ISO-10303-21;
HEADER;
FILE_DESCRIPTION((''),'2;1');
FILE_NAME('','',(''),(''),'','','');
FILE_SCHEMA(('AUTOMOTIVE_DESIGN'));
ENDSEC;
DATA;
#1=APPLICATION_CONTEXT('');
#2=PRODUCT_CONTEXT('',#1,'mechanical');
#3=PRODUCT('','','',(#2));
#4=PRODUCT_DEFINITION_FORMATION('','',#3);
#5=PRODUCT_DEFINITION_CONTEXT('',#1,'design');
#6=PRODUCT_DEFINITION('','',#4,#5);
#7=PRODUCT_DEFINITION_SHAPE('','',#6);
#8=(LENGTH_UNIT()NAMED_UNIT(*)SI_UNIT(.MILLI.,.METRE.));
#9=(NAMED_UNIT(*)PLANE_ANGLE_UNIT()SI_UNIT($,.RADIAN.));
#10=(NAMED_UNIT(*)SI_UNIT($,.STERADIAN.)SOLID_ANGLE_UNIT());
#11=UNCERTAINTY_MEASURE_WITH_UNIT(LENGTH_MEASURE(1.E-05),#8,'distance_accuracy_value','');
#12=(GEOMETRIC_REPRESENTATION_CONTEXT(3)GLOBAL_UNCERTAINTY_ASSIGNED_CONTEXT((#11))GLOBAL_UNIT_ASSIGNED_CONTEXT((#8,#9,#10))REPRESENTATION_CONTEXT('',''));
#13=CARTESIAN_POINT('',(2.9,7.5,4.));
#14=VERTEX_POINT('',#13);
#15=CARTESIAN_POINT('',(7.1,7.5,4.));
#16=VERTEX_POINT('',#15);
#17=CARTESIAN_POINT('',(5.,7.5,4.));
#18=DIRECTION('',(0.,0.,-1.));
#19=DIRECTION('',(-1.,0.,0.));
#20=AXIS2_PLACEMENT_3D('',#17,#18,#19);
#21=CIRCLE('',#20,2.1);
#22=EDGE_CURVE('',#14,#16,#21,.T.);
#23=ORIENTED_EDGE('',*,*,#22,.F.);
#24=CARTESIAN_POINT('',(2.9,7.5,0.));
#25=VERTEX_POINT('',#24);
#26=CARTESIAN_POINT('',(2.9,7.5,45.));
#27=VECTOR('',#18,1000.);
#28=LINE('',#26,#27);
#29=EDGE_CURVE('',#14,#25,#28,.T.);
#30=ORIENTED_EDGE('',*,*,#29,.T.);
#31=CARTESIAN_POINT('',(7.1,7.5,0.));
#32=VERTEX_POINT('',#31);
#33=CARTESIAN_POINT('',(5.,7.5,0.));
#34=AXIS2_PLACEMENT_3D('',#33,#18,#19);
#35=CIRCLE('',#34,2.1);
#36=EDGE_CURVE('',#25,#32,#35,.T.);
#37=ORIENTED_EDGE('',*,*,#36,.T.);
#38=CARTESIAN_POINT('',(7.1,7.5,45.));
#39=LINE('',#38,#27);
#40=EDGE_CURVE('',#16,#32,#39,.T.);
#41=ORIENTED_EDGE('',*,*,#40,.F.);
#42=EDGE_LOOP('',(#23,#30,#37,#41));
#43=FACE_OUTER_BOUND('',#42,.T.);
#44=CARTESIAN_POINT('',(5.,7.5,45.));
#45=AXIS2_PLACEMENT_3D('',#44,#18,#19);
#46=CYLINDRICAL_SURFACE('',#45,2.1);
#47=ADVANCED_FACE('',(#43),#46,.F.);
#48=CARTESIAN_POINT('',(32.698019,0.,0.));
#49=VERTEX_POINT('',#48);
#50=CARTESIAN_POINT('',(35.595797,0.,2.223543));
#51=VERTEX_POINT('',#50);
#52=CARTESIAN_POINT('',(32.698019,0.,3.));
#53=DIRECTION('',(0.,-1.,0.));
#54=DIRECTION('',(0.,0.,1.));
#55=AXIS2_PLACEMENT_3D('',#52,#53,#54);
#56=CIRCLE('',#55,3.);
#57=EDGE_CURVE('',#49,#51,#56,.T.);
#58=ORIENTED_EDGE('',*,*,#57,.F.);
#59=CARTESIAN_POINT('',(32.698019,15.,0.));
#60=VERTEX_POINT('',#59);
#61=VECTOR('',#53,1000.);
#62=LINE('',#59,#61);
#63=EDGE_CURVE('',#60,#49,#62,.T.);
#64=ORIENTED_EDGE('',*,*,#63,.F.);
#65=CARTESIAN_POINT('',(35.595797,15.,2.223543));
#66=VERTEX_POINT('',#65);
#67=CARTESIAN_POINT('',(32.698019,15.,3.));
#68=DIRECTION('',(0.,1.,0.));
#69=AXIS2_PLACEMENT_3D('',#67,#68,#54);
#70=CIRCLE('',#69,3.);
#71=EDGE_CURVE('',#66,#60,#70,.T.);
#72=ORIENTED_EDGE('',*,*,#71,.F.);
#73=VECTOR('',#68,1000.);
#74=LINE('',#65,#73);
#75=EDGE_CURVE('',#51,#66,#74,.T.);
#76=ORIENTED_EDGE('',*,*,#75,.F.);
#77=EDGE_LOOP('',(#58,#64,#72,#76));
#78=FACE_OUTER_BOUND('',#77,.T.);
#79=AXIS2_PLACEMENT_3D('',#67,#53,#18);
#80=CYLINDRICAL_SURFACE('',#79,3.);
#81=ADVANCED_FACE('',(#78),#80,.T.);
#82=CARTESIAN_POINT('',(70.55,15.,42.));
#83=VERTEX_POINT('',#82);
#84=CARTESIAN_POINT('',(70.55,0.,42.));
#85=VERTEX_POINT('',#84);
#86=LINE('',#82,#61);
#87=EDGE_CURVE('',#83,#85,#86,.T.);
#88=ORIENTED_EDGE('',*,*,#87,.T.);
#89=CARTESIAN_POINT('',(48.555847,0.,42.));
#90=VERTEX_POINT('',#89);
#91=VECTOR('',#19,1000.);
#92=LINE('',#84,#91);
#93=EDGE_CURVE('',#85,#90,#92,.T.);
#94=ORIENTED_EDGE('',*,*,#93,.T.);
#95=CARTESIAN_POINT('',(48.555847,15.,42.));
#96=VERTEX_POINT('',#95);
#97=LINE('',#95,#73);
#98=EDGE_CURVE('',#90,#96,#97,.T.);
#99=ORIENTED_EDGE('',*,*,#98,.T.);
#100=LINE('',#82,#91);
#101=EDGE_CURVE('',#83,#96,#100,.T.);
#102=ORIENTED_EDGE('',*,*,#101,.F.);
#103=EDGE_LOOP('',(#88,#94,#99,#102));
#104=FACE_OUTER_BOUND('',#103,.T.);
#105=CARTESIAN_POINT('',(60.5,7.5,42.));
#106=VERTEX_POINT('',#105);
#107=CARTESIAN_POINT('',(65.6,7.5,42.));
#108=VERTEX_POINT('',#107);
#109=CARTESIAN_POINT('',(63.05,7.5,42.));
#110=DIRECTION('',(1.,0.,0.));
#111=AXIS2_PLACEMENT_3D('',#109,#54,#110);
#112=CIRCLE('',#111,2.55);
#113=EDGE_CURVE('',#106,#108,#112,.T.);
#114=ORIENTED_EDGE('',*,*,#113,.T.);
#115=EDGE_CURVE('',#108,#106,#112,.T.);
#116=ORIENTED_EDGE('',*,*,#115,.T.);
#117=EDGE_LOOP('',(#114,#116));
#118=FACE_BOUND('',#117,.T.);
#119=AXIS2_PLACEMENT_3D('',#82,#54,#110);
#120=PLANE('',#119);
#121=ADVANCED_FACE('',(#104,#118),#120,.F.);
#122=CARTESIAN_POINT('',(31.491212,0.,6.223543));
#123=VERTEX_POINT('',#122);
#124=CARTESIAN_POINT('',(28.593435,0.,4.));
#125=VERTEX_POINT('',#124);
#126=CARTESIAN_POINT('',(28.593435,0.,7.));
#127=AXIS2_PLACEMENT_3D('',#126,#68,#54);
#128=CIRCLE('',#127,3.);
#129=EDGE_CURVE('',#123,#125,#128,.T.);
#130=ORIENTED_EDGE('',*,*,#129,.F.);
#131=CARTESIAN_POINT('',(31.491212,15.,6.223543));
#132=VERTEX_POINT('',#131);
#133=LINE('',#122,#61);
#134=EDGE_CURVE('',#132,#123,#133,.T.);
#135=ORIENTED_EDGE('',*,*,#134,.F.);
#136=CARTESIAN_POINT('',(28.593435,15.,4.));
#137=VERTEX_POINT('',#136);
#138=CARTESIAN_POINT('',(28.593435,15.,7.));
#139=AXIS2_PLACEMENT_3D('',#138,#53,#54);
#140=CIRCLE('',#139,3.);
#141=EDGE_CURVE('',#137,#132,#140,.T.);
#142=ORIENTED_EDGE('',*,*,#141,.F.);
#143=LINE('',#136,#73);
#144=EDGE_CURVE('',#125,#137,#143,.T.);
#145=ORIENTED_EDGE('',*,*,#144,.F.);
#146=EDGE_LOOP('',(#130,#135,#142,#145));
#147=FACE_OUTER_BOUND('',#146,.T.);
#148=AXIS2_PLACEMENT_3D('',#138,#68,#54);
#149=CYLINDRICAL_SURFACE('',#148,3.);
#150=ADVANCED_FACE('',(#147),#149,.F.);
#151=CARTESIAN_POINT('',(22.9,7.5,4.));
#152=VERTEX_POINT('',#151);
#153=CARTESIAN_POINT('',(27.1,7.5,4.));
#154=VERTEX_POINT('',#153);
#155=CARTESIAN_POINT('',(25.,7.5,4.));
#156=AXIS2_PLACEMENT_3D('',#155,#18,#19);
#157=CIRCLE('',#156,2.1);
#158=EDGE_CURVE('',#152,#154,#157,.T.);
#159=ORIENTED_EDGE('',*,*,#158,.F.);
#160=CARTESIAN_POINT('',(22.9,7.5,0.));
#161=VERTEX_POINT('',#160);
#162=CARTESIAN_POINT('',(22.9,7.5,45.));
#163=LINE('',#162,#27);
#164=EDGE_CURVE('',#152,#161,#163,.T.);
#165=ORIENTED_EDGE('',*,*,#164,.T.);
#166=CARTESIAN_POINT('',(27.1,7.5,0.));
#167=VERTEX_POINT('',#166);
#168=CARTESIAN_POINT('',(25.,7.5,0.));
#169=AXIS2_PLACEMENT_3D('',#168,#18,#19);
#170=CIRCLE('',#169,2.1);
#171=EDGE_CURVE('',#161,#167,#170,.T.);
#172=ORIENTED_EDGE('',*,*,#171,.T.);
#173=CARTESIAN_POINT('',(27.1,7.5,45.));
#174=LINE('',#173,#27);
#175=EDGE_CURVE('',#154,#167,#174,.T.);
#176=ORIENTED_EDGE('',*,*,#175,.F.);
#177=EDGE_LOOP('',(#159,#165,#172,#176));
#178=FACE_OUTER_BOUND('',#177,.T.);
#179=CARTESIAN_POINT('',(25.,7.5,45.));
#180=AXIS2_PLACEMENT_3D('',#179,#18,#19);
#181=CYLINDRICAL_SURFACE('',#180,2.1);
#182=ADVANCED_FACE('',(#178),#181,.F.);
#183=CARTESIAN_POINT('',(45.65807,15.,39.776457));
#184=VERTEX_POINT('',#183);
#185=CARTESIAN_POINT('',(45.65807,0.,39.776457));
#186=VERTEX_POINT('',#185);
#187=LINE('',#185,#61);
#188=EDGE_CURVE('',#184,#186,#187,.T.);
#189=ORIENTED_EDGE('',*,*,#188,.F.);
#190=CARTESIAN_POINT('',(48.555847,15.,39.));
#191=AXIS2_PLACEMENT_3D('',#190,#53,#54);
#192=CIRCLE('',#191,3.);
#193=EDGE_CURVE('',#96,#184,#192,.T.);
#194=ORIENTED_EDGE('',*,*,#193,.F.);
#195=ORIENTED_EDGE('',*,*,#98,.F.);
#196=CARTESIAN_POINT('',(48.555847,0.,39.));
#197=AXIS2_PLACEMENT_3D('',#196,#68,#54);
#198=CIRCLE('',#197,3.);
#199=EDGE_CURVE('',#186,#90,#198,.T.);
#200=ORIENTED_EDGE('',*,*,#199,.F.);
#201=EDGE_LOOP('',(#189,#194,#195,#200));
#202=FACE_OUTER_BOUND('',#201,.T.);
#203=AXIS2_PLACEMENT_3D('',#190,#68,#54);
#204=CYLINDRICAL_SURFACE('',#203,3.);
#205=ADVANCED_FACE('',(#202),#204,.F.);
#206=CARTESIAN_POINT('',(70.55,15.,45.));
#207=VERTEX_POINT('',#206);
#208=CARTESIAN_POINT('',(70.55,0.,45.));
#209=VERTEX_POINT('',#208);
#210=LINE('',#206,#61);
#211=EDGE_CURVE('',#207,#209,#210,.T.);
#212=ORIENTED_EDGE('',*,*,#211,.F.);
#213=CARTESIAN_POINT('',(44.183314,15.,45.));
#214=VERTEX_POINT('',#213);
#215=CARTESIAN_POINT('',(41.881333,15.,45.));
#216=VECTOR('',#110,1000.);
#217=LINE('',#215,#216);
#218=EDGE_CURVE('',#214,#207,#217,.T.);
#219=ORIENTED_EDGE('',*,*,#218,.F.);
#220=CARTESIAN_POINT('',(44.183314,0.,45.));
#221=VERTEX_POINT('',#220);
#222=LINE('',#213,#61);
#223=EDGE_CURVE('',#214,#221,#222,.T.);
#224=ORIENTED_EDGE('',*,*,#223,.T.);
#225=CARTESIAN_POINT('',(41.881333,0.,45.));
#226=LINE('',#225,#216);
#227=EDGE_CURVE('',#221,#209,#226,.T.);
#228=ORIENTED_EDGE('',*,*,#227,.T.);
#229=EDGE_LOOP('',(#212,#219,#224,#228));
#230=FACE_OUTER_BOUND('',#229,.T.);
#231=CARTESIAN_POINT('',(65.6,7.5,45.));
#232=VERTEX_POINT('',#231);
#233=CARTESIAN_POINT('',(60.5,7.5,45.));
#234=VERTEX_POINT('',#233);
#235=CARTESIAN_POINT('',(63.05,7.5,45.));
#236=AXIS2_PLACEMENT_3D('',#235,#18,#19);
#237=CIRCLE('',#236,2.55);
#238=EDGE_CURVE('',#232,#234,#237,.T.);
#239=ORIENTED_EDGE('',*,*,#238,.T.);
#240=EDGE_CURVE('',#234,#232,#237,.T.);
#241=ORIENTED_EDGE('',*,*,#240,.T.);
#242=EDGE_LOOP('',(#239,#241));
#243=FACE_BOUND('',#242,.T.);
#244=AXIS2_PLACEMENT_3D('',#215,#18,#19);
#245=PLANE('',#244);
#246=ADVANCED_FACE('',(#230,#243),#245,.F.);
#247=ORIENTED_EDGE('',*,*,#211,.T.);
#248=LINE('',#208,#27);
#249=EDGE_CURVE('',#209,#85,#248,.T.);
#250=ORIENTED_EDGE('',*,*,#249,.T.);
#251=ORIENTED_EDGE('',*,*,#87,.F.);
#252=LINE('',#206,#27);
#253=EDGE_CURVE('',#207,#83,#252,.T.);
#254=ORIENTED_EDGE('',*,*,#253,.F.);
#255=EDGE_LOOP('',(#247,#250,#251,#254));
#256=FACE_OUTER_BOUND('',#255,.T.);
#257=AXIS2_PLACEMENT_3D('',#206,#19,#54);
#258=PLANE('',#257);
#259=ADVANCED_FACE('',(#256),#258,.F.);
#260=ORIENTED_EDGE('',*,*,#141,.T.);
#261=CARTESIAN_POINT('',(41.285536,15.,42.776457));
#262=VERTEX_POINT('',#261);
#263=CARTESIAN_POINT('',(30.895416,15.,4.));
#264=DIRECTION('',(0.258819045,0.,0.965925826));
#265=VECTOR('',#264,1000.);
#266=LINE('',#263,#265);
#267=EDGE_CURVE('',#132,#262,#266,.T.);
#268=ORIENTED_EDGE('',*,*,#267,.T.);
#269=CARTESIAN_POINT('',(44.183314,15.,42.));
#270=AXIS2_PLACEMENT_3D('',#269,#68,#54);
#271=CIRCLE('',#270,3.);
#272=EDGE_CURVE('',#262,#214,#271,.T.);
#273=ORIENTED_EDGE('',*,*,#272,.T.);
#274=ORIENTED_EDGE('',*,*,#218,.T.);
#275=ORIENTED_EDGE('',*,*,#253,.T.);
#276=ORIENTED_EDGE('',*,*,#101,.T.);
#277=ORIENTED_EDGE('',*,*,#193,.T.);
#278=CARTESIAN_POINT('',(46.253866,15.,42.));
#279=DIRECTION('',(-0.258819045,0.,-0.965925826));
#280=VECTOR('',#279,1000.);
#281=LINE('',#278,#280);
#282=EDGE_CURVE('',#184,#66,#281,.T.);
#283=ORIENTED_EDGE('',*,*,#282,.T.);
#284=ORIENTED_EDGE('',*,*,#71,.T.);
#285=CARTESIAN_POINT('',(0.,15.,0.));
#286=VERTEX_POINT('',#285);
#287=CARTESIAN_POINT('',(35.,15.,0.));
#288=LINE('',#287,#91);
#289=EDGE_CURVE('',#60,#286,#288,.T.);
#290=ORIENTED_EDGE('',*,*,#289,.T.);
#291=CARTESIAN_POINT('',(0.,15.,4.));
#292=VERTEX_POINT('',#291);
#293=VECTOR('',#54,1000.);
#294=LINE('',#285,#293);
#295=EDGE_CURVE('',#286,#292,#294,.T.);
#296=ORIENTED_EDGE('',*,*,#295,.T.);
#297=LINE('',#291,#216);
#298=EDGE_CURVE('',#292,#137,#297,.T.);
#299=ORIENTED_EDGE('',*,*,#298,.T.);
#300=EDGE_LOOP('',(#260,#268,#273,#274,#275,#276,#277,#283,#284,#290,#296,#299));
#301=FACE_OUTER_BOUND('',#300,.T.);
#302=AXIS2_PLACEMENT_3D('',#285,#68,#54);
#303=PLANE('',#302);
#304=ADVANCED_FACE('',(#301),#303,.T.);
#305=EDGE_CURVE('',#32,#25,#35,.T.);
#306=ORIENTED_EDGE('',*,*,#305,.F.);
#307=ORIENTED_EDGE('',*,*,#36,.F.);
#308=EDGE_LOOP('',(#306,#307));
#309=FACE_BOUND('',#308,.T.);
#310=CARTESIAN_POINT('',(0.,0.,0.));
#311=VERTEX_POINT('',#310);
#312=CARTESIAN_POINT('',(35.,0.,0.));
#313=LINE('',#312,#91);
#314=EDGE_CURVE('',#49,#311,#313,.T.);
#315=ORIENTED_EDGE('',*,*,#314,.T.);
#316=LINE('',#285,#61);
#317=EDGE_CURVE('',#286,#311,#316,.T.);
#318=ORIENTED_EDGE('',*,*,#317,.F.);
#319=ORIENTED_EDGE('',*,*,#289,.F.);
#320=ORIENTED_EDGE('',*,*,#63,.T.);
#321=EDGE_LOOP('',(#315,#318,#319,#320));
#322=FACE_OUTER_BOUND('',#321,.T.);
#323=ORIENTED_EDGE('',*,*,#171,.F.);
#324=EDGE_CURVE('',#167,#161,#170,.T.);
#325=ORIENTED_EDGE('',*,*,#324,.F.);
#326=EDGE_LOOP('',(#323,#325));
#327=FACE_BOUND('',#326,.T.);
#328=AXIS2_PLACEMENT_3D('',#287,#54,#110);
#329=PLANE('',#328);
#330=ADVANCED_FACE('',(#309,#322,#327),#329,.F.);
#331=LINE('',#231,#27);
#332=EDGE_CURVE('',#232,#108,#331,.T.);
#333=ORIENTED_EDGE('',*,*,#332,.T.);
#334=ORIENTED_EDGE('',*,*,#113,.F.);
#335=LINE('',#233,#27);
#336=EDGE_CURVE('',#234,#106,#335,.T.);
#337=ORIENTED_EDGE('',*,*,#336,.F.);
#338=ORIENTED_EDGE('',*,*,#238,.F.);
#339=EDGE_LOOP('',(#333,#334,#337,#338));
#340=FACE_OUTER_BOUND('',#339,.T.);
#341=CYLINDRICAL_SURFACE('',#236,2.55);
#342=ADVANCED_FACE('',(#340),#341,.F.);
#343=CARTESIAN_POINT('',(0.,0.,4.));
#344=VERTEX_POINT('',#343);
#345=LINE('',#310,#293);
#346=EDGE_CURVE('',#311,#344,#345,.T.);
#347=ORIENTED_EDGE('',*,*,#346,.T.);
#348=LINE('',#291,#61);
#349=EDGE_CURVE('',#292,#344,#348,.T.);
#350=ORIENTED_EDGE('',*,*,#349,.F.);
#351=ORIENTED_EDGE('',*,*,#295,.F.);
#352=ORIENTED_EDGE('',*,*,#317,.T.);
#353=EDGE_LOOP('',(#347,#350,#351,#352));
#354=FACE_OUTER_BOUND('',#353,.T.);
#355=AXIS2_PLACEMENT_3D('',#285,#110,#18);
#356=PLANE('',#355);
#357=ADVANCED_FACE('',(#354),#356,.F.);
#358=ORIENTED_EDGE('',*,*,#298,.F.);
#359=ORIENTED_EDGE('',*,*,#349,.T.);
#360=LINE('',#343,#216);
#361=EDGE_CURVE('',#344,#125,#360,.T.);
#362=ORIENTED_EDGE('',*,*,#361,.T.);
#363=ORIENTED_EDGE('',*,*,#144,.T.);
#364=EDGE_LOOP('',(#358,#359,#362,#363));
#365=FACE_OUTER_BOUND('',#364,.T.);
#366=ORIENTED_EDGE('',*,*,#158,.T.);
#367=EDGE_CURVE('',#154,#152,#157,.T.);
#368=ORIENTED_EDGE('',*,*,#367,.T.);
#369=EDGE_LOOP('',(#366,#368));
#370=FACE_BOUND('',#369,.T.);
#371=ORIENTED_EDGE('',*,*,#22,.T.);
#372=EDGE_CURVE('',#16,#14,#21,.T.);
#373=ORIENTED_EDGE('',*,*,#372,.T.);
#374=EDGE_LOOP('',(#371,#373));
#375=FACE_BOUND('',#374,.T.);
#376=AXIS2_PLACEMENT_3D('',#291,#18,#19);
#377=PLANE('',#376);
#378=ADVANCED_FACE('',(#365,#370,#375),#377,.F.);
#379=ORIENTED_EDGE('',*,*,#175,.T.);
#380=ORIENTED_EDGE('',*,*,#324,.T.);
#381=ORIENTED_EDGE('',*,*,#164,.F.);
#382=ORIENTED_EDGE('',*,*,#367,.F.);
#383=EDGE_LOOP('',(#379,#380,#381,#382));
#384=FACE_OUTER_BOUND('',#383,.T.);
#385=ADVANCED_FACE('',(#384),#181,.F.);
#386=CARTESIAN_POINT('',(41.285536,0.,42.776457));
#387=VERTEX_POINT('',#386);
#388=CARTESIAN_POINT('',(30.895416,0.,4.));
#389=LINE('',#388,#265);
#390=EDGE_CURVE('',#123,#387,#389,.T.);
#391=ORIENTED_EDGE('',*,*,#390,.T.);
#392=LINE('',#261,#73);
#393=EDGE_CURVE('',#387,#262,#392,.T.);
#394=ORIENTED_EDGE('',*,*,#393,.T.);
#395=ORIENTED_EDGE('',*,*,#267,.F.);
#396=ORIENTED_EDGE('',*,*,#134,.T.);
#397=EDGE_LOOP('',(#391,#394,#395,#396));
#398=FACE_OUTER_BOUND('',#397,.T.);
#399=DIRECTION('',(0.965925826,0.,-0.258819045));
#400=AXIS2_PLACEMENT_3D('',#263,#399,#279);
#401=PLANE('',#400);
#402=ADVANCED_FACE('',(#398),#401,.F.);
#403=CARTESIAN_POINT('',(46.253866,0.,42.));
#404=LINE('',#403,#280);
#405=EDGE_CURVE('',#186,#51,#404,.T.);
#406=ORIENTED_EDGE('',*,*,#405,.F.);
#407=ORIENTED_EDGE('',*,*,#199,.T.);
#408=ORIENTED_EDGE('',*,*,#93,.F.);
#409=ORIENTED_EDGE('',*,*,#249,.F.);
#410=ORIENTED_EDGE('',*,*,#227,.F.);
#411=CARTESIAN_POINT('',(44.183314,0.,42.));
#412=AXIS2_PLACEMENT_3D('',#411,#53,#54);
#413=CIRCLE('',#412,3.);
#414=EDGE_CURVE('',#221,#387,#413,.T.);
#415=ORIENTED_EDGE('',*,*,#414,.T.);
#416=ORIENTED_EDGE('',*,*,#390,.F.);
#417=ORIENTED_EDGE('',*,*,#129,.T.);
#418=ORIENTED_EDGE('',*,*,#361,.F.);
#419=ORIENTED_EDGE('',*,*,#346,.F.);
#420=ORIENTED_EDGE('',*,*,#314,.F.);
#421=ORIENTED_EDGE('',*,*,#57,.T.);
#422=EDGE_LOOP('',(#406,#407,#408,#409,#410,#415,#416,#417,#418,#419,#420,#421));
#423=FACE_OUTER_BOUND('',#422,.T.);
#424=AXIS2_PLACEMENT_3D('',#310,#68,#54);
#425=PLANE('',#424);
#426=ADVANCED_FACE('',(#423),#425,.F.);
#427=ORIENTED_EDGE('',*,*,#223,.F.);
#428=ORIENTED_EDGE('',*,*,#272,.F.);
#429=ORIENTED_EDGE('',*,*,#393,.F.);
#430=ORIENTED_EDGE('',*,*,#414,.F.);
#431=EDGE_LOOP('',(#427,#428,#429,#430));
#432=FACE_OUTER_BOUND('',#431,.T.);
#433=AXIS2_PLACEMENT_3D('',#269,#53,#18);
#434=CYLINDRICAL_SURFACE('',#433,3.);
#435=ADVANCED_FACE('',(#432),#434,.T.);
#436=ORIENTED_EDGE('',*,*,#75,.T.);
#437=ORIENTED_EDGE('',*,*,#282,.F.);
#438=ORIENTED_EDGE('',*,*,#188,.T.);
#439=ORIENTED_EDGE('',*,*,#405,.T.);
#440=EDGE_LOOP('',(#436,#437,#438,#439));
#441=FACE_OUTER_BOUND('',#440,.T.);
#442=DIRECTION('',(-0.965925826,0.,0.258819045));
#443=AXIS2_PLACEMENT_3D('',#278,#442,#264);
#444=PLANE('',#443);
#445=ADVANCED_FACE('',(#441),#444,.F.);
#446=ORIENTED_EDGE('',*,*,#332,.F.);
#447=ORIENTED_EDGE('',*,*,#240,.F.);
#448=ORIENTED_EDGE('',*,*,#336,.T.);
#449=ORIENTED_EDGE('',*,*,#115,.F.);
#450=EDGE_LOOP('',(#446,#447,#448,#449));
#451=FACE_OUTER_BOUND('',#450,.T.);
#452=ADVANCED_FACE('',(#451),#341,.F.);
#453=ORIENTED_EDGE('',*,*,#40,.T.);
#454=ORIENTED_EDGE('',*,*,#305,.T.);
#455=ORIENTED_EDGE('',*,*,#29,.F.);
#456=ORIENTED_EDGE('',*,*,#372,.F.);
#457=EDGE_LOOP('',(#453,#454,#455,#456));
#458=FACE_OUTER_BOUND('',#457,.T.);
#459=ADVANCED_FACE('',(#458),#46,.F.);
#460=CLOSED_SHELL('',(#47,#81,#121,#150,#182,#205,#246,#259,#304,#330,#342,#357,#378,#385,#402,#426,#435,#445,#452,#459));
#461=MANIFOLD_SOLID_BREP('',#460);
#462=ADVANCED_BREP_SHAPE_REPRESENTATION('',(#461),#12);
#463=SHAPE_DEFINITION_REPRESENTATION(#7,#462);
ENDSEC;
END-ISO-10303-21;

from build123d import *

# Parameters (mm, degrees)
EXTRUDE_1_DEPTH          = 15
CUT_EXTRUDE_1_DEPTH      = 84.464378629
CUT_EXTRUDE_1_DEPTH_BACK = 84.464378629
SKETCH_2_R               = 2.55
SKETCH_2_R_2             = 2.1
FILLET_1_R               = 3


with BuildPart() as part:
    # 草图1 → 凸台-拉伸1 (new body)
    with BuildSketch(Plane(origin=(0, 0, 0), x_dir=(1, 0, 0), z_dir=(0, 1, 0))):
        Polygon((0, 0), (0, -4), (30.895415868, -4), (41.881332757, -45), (70.55, -45), (70.55, -42), (46.253866082, -42), (35, 0), align=None)
    extrude(amount=EXTRUDE_1_DEPTH)

    # 草图2 → 切除-拉伸1 (cut, two sides: drawn at the far end of the back side and taken through both)
    with BuildSketch(Plane(origin=(0, 0, 42), x_dir=(-1, 0, 0), z_dir=(0, 0, -1)).offset(-CUT_EXTRUDE_1_DEPTH_BACK)):
        with Locations((-63.05, 7.5)):
            Circle(SKETCH_2_R)
        with Locations((-25, 7.5)):
            Circle(SKETCH_2_R_2)
        with Locations((-5, 7.5)):
            Circle(SKETCH_2_R_2)
    extrude(amount=CUT_EXTRUDE_1_DEPTH + CUT_EXTRUDE_1_DEPTH_BACK, mode=Mode.SUBTRACT)

    # 圆角1
    fillet_1_edges = [part.edges().sort_by_distance(p)[0] for p in [
        (35, 7.5, 0),
        (46.253866082, 7.5, 42),
        (41.881332757, 7.5, 45),
        (30.895415868, 7.5, 4),
    ]]
    fillet(fillet_1_edges, radius=FILLET_1_R)


solid = part.part
